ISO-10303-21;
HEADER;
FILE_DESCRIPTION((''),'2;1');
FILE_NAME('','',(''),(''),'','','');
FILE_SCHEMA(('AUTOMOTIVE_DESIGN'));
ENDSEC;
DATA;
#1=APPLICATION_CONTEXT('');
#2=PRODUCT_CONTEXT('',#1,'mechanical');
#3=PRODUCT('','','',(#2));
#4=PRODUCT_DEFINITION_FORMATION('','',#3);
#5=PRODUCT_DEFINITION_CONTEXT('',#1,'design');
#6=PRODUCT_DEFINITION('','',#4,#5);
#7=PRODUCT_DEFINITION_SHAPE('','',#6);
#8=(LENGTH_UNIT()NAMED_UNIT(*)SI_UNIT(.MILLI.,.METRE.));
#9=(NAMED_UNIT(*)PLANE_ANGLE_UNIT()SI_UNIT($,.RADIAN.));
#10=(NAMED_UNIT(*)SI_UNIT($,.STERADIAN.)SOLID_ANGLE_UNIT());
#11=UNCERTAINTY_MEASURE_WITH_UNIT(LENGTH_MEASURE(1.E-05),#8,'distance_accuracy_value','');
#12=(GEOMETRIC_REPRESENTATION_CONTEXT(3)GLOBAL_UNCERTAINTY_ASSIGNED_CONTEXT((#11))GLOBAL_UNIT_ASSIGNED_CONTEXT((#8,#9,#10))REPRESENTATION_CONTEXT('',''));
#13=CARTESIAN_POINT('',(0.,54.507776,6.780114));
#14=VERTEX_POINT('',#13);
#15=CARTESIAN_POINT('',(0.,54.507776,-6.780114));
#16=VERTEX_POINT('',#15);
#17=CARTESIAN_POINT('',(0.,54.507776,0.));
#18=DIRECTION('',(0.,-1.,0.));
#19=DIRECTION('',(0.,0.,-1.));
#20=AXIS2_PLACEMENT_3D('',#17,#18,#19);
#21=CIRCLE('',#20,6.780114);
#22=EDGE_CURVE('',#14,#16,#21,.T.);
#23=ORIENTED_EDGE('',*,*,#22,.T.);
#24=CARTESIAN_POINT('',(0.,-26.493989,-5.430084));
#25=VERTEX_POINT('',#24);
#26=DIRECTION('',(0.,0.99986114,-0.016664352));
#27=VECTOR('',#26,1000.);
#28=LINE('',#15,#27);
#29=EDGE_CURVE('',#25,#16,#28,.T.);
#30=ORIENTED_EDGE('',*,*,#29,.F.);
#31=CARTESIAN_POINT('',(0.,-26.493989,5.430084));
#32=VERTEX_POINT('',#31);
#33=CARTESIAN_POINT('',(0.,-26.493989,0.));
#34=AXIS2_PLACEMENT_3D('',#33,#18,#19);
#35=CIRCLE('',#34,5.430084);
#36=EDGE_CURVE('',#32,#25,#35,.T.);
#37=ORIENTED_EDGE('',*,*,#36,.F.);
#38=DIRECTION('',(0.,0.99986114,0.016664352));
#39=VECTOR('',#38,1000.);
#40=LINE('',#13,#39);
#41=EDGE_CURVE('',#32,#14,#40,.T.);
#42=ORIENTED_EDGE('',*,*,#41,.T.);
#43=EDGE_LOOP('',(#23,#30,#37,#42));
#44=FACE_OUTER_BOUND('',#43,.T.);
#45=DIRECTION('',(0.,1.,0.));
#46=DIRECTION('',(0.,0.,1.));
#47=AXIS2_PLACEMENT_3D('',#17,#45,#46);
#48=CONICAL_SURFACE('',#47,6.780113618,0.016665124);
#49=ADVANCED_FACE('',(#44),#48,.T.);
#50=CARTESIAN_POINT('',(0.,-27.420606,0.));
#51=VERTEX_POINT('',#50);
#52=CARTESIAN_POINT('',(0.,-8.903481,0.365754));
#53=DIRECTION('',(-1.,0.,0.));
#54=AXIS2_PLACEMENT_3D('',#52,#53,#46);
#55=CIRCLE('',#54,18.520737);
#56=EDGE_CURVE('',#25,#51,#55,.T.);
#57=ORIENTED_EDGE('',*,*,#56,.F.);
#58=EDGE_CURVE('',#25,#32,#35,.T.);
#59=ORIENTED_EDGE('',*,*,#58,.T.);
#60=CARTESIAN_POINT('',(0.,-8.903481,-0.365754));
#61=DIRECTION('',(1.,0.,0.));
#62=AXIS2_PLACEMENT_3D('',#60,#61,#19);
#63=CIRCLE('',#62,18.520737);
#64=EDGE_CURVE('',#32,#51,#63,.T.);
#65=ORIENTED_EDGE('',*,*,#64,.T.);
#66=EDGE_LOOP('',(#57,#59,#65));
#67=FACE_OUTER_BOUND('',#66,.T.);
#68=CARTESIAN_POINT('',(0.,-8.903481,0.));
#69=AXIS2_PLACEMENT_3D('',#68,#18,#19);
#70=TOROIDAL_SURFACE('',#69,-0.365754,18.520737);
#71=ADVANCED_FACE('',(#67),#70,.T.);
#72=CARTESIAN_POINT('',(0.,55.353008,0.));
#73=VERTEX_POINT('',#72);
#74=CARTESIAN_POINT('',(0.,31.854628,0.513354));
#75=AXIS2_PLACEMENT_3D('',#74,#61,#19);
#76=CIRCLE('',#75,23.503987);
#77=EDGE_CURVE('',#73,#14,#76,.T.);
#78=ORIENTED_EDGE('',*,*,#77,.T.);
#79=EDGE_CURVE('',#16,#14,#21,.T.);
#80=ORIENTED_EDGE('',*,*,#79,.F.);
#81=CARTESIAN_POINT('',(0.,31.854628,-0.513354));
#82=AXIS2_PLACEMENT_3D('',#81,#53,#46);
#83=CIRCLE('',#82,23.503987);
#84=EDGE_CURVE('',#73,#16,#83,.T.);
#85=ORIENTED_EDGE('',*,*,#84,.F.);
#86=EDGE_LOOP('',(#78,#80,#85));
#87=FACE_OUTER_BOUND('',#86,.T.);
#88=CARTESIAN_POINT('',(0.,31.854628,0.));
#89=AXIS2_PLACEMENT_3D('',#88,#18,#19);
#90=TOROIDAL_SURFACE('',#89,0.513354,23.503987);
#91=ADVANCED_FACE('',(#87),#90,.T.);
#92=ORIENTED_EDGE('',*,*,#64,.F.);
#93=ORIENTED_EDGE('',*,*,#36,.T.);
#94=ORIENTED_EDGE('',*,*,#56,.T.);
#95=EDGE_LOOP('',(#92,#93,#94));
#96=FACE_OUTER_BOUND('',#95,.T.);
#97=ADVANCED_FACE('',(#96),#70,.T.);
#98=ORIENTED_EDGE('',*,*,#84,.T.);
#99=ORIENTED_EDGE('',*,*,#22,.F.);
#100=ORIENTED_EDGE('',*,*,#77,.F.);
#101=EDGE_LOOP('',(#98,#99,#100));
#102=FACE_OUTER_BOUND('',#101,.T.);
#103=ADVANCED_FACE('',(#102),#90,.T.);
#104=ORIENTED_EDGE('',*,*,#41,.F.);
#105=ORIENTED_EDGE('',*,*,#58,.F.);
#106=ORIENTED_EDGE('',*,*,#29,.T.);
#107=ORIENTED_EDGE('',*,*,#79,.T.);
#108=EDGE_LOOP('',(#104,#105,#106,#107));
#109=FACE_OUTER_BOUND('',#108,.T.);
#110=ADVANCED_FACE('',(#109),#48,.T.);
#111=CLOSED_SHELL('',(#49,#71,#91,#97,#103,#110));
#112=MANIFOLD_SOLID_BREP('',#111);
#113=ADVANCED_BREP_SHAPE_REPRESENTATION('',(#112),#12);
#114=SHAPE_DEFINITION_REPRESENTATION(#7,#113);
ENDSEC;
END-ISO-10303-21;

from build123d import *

# Parameters (mm, degrees)
SCALE_1_SCALE = 1.875


with BuildPart() as part:
    # Sketch1 → Revolve1 (revolve)
    with BuildSketch(Plane.XY, mode=Mode.PRIVATE) as revolve1_sk:
        with BuildLine():
            Line((-3.616060596, 37.025813588), (-2.896044906, -6.175127807))
            ThreePointArc((-2.896044906, -6.175127807), (-1.466498616, -6.530498208), (0, -6.669323733))
            Line((0, -6.669323733), (0, 0))
            Line((0, 0), (0, 30.062177826))
            Line((0, 30.062177826), (0, 37.476603875))
            ThreePointArc((0, 37.476603875), (-1.8244983, 37.383308497), (-3.616060596, 37.025813588))
        make_face()
    revolve(revolve1_sk.sketch.rotate(Axis((0, 0, 0), (0, 1, 0)), 270), axis=Axis((0, 0, 0), (0, 1, 0)))


with BuildPart() as part_1:
    # Scale 1: scaled about (0, 17.046427659, 0)
    add(part.part.scale(SCALE_1_SCALE).moved(Location((0, -14.915624202, 0))))


solid = part_1.part
